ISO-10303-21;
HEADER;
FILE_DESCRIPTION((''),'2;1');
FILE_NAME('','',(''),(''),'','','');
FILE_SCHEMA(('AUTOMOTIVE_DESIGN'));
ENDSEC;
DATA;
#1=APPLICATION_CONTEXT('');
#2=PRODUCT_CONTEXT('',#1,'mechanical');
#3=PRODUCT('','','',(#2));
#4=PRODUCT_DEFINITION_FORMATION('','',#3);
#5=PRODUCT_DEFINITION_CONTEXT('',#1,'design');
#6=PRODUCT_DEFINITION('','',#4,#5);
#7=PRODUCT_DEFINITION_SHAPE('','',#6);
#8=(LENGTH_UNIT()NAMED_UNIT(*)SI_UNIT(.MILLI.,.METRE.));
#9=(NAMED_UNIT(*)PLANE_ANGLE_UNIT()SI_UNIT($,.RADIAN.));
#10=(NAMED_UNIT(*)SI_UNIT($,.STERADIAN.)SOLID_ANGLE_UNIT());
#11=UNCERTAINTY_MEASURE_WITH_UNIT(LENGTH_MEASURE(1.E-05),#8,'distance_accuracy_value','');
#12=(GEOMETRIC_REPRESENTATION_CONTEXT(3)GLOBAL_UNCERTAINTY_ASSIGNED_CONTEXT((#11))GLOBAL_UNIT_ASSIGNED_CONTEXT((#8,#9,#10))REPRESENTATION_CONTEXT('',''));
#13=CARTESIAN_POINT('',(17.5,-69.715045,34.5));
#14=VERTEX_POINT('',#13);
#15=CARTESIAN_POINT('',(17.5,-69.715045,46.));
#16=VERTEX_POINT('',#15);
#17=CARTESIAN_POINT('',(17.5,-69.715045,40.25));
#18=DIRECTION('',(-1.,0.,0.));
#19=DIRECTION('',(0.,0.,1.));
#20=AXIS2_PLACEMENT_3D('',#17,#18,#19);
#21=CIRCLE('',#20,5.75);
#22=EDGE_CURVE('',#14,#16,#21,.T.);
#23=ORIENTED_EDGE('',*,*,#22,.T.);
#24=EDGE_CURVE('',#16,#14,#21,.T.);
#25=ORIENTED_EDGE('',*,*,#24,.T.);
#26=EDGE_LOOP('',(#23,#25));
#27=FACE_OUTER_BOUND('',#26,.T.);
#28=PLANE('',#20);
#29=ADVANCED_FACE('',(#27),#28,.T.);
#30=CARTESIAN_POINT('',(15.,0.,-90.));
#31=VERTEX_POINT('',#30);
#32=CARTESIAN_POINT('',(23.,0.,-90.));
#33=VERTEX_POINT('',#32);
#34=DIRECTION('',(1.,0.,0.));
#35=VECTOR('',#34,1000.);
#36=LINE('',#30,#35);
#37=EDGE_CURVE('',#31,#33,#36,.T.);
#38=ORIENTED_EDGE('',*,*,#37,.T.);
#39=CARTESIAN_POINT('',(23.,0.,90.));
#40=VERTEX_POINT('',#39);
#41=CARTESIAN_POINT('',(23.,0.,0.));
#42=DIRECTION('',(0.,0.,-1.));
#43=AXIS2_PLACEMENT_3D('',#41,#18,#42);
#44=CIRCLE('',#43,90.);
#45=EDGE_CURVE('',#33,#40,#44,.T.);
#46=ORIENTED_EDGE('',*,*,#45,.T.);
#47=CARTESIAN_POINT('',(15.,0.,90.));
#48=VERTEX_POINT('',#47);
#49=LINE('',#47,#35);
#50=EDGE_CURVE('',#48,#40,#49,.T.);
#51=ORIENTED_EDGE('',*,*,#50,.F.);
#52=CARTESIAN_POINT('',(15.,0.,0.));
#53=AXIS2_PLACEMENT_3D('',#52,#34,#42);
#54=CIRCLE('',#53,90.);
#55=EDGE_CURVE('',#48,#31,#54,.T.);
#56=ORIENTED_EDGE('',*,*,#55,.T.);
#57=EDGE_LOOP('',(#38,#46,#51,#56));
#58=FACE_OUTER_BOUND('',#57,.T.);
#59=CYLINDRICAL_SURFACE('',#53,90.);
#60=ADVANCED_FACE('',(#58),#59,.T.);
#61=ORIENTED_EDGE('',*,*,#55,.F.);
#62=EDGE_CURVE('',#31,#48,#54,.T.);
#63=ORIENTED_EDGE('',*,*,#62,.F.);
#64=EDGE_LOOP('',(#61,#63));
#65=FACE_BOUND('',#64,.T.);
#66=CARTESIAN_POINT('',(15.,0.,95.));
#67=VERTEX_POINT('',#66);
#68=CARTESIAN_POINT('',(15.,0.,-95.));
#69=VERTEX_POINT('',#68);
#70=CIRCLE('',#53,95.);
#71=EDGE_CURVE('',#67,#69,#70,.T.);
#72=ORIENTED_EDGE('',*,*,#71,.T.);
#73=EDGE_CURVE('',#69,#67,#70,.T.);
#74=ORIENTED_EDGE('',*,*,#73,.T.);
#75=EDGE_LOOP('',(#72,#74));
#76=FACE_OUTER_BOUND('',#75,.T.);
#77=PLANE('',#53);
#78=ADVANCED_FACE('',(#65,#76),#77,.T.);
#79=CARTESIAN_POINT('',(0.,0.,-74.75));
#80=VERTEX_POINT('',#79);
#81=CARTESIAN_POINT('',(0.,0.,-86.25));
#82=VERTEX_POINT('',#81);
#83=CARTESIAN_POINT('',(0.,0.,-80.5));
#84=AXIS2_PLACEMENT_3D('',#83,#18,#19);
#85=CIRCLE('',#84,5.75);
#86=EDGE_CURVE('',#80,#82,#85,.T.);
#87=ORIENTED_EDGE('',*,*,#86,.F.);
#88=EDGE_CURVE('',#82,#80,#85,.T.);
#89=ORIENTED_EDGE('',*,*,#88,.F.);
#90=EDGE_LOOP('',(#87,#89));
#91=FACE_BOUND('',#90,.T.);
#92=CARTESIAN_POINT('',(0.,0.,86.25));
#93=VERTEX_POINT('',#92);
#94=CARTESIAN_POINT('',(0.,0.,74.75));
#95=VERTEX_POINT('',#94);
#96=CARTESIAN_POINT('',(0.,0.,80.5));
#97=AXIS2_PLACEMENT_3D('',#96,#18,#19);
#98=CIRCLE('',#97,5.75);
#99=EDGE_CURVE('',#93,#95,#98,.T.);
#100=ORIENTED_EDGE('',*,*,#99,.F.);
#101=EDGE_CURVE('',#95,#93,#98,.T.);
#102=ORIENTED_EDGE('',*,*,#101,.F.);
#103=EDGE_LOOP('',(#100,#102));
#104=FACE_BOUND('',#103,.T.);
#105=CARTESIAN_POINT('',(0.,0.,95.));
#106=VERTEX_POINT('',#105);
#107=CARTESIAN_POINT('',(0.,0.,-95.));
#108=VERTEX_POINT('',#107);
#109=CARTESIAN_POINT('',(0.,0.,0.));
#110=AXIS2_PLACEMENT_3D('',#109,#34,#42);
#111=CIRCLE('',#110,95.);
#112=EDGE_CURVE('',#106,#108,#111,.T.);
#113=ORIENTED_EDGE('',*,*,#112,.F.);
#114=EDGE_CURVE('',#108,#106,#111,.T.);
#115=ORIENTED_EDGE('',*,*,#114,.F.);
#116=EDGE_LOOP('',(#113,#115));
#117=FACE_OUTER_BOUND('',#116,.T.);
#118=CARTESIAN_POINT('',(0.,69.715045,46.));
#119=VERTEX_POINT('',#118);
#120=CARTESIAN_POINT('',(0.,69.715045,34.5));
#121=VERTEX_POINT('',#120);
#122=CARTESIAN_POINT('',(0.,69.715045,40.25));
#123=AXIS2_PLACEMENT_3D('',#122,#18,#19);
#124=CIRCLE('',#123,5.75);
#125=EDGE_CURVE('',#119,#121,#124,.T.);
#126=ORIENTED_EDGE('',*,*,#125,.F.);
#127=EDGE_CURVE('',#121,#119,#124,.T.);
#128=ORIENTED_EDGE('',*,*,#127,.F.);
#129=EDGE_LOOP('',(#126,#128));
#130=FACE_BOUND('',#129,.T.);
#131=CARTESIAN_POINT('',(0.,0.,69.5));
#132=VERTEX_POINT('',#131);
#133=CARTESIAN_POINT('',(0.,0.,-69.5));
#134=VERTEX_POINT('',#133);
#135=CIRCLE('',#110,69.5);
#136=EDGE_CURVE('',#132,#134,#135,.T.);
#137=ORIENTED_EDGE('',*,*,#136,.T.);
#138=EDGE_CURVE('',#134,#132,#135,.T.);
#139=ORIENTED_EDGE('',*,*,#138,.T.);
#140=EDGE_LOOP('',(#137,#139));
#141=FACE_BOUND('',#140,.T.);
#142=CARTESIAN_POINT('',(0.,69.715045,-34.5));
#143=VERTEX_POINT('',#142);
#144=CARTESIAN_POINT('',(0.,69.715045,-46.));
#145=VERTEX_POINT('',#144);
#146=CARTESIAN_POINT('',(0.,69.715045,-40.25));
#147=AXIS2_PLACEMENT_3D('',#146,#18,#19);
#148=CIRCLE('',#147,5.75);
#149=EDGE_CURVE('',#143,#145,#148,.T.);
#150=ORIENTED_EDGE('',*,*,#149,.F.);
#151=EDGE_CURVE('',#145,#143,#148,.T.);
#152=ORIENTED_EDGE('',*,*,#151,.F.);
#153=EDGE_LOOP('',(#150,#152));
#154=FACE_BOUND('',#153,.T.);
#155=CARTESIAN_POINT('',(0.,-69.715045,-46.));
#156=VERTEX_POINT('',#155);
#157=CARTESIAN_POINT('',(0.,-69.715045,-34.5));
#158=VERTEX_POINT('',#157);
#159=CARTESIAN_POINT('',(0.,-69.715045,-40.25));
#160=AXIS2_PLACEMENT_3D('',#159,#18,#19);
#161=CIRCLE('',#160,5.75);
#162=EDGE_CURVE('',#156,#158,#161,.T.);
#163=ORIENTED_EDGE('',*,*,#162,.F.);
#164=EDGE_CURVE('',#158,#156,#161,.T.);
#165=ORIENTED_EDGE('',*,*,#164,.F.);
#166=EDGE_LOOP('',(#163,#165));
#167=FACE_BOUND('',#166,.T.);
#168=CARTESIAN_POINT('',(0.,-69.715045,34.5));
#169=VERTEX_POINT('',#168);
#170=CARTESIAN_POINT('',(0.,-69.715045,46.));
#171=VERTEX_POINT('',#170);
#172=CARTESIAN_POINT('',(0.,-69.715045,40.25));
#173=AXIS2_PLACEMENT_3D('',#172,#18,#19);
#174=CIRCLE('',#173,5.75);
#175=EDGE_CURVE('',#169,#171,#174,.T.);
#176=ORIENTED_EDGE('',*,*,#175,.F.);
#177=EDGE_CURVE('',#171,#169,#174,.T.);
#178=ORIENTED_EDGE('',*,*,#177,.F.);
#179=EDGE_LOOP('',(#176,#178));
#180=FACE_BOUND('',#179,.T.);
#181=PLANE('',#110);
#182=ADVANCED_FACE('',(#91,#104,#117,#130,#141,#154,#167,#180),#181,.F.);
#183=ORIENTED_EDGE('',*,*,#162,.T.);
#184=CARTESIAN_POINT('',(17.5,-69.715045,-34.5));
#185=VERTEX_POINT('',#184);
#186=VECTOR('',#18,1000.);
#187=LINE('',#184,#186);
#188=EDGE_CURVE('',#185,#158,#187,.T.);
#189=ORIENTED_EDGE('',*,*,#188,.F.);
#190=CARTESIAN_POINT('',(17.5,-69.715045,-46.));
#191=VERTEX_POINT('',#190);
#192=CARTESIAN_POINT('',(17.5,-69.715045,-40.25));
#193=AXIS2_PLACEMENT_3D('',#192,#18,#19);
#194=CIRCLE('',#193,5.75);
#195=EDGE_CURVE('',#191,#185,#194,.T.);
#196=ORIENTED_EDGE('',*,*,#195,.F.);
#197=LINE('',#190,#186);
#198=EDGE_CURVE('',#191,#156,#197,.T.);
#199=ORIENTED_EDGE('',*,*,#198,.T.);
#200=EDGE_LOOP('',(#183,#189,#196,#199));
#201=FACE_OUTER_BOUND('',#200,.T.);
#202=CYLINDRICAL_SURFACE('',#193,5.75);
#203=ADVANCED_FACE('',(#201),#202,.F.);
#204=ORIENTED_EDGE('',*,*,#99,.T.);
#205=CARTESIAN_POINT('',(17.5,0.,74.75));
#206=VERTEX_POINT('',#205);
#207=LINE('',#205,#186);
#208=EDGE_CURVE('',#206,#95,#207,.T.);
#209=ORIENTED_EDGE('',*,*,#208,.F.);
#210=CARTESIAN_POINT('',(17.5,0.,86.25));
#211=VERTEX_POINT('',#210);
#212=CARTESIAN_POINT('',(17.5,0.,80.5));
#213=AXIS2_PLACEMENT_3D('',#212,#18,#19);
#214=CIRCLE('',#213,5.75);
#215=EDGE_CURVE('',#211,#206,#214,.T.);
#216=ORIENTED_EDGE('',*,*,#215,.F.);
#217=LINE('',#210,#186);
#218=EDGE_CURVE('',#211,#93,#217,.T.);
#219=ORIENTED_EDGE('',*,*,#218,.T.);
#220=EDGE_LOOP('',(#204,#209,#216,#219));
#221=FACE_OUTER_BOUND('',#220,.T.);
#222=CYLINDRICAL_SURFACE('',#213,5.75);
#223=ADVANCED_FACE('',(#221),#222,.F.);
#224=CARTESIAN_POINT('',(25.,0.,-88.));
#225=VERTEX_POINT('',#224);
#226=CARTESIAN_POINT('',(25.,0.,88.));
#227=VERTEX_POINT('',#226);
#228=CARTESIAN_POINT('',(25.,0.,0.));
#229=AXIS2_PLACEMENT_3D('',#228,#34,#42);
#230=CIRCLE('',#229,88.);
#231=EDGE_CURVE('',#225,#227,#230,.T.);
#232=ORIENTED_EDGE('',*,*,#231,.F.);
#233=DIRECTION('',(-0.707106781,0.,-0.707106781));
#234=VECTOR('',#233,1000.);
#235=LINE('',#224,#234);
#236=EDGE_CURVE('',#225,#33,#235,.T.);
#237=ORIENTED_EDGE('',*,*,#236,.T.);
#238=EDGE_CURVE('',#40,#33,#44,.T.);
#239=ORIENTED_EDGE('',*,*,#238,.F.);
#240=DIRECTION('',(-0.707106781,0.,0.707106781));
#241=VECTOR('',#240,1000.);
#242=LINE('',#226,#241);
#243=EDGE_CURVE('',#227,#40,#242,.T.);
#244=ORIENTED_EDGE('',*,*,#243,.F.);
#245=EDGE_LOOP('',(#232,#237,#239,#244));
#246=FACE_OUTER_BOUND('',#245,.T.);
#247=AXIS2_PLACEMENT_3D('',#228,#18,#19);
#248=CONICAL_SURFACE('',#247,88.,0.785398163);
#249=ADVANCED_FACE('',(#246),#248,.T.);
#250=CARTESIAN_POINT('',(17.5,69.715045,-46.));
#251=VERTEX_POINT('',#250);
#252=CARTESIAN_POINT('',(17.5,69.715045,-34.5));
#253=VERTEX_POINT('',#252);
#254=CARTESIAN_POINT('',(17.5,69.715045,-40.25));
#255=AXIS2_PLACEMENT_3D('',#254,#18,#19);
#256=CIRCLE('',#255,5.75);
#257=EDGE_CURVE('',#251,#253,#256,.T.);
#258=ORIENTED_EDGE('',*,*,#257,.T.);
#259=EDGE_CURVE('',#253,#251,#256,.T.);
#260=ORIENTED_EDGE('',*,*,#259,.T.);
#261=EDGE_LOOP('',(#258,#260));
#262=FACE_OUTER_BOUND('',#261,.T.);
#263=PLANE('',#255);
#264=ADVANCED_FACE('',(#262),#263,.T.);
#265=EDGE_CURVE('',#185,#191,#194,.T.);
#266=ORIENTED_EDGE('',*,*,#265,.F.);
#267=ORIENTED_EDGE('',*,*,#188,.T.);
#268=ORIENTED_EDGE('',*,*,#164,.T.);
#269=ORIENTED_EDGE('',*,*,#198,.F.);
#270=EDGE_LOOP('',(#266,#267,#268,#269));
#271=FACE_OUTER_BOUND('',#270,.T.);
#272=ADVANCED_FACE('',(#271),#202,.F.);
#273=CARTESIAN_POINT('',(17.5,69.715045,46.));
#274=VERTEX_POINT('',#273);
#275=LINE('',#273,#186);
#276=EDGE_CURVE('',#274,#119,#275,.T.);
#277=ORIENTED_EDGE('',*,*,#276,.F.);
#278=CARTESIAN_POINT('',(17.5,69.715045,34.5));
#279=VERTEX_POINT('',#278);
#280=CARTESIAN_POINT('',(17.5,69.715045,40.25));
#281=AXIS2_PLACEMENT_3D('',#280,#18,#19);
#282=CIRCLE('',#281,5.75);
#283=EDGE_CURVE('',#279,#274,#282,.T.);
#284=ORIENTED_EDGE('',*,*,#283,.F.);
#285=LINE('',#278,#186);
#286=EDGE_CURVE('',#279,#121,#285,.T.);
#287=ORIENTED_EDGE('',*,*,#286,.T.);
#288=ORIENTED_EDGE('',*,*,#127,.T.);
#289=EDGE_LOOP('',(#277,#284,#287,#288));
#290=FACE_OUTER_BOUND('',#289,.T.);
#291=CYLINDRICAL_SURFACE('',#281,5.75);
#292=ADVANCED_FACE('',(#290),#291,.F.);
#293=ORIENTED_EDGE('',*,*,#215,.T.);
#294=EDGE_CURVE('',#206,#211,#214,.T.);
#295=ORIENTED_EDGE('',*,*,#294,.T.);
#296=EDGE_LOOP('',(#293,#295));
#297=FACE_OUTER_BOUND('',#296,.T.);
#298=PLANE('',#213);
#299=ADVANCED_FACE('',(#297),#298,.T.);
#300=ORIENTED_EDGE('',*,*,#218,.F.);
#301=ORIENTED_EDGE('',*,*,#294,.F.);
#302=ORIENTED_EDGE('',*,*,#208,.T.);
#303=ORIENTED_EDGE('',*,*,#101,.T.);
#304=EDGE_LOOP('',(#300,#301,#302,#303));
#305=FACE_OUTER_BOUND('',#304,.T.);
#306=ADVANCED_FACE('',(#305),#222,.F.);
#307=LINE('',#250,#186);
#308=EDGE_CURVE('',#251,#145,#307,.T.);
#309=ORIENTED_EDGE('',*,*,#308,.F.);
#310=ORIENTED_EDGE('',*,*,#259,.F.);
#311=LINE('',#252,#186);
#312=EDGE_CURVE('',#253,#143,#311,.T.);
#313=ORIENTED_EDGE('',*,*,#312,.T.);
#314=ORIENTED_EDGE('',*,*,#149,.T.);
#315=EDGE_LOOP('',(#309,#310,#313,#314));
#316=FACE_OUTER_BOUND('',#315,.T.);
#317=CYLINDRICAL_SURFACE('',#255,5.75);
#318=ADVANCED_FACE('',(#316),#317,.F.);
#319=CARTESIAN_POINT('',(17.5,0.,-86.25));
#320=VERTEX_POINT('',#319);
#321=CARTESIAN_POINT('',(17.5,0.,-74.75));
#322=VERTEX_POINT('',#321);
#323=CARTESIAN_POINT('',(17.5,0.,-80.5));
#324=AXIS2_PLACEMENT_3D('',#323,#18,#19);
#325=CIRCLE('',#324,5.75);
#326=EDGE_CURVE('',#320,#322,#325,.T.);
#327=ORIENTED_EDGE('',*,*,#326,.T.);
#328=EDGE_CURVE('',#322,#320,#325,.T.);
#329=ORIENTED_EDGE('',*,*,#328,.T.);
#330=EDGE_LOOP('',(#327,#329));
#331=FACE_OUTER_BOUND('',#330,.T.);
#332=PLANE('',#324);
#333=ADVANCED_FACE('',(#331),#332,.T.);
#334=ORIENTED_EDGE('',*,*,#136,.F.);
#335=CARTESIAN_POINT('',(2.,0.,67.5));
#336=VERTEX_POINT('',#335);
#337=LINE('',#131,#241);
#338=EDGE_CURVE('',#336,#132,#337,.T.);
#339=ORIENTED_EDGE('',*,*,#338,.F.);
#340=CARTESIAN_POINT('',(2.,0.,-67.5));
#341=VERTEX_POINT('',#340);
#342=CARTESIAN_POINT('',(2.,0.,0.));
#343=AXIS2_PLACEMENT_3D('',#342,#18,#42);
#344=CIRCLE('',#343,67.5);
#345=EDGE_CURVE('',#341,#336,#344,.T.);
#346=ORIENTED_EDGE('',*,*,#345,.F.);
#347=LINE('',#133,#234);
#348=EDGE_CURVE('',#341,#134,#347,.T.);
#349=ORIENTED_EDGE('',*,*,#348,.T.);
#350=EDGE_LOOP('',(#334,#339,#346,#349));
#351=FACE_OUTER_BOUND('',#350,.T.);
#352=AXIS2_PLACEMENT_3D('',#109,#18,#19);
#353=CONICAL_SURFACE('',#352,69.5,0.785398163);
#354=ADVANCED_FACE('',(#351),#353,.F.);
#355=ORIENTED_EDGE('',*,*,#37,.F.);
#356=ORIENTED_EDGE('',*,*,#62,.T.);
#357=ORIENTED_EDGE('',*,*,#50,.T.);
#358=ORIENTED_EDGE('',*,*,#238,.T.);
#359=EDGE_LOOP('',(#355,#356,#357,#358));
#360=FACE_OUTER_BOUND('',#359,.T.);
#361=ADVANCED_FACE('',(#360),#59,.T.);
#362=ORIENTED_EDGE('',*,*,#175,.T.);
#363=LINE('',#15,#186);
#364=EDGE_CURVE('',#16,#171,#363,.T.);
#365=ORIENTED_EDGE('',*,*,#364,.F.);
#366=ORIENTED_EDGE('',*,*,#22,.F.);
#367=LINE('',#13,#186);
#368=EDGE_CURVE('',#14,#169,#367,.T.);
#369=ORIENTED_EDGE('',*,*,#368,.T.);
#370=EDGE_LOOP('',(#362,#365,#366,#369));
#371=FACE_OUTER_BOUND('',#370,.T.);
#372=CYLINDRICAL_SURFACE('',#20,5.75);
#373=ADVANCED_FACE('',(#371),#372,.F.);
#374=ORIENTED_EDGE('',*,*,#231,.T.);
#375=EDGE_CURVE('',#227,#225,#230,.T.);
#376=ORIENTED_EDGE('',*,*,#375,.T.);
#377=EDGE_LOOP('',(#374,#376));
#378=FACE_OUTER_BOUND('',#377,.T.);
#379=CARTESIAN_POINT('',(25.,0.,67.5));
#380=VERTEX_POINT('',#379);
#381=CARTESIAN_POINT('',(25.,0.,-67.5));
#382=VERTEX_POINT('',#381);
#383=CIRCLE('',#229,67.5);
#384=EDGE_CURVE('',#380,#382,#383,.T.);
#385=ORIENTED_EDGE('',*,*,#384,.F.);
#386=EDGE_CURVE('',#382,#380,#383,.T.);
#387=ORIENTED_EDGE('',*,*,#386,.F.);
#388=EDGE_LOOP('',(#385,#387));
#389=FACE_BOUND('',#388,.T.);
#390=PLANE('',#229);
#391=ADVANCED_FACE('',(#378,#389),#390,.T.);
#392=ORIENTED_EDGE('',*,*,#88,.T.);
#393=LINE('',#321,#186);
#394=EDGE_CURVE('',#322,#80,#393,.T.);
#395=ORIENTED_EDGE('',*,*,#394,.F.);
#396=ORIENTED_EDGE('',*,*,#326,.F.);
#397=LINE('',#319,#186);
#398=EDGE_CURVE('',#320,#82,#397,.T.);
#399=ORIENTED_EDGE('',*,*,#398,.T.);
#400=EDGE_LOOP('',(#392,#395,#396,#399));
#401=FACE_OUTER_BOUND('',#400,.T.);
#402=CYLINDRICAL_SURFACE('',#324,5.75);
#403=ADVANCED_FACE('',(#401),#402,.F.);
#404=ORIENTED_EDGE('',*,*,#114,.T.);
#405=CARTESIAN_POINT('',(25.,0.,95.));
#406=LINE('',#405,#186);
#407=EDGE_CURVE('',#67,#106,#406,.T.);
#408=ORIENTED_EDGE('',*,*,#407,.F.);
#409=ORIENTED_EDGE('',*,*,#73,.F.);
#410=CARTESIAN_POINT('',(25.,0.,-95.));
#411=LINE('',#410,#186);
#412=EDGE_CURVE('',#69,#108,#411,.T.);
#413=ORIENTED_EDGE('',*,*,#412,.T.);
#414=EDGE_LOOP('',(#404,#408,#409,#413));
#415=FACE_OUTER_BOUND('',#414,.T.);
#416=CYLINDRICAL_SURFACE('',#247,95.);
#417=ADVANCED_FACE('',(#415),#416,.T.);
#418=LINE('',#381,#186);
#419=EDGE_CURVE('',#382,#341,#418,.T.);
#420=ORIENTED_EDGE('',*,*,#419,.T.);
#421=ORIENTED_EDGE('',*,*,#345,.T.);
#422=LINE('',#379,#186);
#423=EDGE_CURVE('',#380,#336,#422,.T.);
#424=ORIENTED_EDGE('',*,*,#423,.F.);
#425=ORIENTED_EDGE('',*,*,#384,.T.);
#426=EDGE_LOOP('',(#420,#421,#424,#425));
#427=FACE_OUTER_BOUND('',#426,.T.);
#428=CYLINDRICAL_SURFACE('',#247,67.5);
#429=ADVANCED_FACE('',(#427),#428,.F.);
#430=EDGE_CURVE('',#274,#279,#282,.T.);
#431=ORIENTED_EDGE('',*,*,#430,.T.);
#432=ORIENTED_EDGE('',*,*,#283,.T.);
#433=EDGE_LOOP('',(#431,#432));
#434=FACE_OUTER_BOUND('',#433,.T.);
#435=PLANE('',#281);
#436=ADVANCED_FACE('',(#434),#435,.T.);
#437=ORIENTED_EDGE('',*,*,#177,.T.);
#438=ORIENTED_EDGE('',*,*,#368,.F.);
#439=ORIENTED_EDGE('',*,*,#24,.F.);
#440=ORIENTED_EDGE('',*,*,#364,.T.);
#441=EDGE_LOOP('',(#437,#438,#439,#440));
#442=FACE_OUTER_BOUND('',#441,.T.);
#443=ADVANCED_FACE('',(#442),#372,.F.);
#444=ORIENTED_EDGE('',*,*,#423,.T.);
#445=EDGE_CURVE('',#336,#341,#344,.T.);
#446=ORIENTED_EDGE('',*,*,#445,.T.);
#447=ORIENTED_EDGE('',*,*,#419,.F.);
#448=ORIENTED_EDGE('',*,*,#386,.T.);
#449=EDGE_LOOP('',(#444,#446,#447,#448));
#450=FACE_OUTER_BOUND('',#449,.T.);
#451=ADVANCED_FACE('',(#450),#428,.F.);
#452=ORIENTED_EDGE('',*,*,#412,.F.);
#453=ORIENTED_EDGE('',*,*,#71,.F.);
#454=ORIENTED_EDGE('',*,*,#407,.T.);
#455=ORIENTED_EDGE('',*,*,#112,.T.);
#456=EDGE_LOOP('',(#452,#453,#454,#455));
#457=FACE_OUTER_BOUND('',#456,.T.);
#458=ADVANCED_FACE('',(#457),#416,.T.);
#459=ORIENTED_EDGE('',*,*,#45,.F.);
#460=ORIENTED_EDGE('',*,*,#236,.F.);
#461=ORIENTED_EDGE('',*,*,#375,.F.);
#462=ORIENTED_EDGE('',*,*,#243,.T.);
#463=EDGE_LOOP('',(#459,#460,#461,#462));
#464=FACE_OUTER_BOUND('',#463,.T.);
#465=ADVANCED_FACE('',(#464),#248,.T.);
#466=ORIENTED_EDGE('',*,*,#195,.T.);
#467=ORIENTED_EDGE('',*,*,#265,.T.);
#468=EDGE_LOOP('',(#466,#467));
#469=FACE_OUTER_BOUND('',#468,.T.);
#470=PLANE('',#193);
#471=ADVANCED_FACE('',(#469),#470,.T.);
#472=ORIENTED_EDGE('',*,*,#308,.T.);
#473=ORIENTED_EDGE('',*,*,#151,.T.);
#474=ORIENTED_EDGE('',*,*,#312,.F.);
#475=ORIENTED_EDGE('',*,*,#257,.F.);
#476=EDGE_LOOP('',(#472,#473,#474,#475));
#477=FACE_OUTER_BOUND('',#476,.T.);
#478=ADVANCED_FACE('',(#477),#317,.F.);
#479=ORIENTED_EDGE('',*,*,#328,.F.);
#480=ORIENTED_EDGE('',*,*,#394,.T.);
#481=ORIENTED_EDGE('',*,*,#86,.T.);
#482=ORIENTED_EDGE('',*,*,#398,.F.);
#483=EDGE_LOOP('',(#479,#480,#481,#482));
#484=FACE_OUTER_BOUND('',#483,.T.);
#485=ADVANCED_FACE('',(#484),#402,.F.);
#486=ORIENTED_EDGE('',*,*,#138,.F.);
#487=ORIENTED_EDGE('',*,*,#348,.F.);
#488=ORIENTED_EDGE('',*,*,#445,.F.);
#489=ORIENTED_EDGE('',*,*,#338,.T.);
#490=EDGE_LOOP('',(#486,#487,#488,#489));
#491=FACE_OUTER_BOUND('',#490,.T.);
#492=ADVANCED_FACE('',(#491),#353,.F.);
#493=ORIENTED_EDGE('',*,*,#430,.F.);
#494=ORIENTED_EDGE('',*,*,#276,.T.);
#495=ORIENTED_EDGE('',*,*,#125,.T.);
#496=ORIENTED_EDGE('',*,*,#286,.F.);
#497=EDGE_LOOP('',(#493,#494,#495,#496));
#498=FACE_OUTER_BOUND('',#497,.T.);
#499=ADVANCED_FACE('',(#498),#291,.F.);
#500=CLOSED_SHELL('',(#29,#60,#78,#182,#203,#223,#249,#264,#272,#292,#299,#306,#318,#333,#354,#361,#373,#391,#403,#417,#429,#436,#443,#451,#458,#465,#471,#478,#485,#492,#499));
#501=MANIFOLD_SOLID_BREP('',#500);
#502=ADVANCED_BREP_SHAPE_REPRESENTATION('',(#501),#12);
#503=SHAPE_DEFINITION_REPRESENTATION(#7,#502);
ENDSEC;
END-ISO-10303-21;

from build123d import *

# Parameters (mm, degrees)
SKETCH1_R           = 95
SKETCH1_R_2         = 67.5
BOSS_EXTRUDE1_DEPTH = 25
CUT_EXTRUDE1_START  = -10
SKETCH2_R           = 95
SKETCH2_R_2         = 90
CUT_EXTRUDE1_DEPTH  = 10
SKETCH3_R           = 5.75
CUT_EXTRUDE2_DEPTH  = 17.5
CHAMFER1_SIZE       = 2


with BuildPart() as part:
    # Sketch1 → Boss-Extrude1 (new body)
    with BuildSketch(Plane(origin=(0, 0, 0), x_dir=(0, 0, -1), z_dir=(1, 0, 0))):
        Circle(SKETCH1_R)
        Circle(SKETCH1_R_2, mode=Mode.SUBTRACT)
    extrude(amount=BOSS_EXTRUDE1_DEPTH)

    # Sketch2 → Cut-Extrude1 (cut)
    with BuildSketch(Plane(origin=(25, 0, 0), x_dir=(0, 0, -1), z_dir=(1, 0, 0)).offset(CUT_EXTRUDE1_START)):
        Circle(SKETCH2_R)
        Circle(SKETCH2_R_2, mode=Mode.SUBTRACT)
    extrude(amount=CUT_EXTRUDE1_DEPTH, mode=Mode.SUBTRACT)

    # Sketch3 → Cut-Extrude2 (cut)
    with BuildSketch(Plane.ZY):
        with Locations((40.25, -69.715045005)):
            Circle(SKETCH3_R)
        with Locations((80.5, 0)):
            Circle(SKETCH3_R)
        with Locations((-40.25, -69.715045005)):
            Circle(SKETCH3_R)
        with Locations((-80.5, 0)):
            Circle(SKETCH3_R)
        with Locations((-40.25, 69.715045005)):
            Circle(SKETCH3_R)
        with Locations((40.25, 69.715045005)):
            Circle(SKETCH3_R)
    extrude(amount=-CUT_EXTRUDE2_DEPTH, mode=Mode.SUBTRACT)

    # Chamfer1
    chamfer1_edges = [part.edges().sort_by_distance(p)[0] for p in [
        (25, 0, 90),
        (0, 0, 67.5),
    ]]
    chamfer(chamfer1_edges, length=CHAMFER1_SIZE)


solid = part.part
